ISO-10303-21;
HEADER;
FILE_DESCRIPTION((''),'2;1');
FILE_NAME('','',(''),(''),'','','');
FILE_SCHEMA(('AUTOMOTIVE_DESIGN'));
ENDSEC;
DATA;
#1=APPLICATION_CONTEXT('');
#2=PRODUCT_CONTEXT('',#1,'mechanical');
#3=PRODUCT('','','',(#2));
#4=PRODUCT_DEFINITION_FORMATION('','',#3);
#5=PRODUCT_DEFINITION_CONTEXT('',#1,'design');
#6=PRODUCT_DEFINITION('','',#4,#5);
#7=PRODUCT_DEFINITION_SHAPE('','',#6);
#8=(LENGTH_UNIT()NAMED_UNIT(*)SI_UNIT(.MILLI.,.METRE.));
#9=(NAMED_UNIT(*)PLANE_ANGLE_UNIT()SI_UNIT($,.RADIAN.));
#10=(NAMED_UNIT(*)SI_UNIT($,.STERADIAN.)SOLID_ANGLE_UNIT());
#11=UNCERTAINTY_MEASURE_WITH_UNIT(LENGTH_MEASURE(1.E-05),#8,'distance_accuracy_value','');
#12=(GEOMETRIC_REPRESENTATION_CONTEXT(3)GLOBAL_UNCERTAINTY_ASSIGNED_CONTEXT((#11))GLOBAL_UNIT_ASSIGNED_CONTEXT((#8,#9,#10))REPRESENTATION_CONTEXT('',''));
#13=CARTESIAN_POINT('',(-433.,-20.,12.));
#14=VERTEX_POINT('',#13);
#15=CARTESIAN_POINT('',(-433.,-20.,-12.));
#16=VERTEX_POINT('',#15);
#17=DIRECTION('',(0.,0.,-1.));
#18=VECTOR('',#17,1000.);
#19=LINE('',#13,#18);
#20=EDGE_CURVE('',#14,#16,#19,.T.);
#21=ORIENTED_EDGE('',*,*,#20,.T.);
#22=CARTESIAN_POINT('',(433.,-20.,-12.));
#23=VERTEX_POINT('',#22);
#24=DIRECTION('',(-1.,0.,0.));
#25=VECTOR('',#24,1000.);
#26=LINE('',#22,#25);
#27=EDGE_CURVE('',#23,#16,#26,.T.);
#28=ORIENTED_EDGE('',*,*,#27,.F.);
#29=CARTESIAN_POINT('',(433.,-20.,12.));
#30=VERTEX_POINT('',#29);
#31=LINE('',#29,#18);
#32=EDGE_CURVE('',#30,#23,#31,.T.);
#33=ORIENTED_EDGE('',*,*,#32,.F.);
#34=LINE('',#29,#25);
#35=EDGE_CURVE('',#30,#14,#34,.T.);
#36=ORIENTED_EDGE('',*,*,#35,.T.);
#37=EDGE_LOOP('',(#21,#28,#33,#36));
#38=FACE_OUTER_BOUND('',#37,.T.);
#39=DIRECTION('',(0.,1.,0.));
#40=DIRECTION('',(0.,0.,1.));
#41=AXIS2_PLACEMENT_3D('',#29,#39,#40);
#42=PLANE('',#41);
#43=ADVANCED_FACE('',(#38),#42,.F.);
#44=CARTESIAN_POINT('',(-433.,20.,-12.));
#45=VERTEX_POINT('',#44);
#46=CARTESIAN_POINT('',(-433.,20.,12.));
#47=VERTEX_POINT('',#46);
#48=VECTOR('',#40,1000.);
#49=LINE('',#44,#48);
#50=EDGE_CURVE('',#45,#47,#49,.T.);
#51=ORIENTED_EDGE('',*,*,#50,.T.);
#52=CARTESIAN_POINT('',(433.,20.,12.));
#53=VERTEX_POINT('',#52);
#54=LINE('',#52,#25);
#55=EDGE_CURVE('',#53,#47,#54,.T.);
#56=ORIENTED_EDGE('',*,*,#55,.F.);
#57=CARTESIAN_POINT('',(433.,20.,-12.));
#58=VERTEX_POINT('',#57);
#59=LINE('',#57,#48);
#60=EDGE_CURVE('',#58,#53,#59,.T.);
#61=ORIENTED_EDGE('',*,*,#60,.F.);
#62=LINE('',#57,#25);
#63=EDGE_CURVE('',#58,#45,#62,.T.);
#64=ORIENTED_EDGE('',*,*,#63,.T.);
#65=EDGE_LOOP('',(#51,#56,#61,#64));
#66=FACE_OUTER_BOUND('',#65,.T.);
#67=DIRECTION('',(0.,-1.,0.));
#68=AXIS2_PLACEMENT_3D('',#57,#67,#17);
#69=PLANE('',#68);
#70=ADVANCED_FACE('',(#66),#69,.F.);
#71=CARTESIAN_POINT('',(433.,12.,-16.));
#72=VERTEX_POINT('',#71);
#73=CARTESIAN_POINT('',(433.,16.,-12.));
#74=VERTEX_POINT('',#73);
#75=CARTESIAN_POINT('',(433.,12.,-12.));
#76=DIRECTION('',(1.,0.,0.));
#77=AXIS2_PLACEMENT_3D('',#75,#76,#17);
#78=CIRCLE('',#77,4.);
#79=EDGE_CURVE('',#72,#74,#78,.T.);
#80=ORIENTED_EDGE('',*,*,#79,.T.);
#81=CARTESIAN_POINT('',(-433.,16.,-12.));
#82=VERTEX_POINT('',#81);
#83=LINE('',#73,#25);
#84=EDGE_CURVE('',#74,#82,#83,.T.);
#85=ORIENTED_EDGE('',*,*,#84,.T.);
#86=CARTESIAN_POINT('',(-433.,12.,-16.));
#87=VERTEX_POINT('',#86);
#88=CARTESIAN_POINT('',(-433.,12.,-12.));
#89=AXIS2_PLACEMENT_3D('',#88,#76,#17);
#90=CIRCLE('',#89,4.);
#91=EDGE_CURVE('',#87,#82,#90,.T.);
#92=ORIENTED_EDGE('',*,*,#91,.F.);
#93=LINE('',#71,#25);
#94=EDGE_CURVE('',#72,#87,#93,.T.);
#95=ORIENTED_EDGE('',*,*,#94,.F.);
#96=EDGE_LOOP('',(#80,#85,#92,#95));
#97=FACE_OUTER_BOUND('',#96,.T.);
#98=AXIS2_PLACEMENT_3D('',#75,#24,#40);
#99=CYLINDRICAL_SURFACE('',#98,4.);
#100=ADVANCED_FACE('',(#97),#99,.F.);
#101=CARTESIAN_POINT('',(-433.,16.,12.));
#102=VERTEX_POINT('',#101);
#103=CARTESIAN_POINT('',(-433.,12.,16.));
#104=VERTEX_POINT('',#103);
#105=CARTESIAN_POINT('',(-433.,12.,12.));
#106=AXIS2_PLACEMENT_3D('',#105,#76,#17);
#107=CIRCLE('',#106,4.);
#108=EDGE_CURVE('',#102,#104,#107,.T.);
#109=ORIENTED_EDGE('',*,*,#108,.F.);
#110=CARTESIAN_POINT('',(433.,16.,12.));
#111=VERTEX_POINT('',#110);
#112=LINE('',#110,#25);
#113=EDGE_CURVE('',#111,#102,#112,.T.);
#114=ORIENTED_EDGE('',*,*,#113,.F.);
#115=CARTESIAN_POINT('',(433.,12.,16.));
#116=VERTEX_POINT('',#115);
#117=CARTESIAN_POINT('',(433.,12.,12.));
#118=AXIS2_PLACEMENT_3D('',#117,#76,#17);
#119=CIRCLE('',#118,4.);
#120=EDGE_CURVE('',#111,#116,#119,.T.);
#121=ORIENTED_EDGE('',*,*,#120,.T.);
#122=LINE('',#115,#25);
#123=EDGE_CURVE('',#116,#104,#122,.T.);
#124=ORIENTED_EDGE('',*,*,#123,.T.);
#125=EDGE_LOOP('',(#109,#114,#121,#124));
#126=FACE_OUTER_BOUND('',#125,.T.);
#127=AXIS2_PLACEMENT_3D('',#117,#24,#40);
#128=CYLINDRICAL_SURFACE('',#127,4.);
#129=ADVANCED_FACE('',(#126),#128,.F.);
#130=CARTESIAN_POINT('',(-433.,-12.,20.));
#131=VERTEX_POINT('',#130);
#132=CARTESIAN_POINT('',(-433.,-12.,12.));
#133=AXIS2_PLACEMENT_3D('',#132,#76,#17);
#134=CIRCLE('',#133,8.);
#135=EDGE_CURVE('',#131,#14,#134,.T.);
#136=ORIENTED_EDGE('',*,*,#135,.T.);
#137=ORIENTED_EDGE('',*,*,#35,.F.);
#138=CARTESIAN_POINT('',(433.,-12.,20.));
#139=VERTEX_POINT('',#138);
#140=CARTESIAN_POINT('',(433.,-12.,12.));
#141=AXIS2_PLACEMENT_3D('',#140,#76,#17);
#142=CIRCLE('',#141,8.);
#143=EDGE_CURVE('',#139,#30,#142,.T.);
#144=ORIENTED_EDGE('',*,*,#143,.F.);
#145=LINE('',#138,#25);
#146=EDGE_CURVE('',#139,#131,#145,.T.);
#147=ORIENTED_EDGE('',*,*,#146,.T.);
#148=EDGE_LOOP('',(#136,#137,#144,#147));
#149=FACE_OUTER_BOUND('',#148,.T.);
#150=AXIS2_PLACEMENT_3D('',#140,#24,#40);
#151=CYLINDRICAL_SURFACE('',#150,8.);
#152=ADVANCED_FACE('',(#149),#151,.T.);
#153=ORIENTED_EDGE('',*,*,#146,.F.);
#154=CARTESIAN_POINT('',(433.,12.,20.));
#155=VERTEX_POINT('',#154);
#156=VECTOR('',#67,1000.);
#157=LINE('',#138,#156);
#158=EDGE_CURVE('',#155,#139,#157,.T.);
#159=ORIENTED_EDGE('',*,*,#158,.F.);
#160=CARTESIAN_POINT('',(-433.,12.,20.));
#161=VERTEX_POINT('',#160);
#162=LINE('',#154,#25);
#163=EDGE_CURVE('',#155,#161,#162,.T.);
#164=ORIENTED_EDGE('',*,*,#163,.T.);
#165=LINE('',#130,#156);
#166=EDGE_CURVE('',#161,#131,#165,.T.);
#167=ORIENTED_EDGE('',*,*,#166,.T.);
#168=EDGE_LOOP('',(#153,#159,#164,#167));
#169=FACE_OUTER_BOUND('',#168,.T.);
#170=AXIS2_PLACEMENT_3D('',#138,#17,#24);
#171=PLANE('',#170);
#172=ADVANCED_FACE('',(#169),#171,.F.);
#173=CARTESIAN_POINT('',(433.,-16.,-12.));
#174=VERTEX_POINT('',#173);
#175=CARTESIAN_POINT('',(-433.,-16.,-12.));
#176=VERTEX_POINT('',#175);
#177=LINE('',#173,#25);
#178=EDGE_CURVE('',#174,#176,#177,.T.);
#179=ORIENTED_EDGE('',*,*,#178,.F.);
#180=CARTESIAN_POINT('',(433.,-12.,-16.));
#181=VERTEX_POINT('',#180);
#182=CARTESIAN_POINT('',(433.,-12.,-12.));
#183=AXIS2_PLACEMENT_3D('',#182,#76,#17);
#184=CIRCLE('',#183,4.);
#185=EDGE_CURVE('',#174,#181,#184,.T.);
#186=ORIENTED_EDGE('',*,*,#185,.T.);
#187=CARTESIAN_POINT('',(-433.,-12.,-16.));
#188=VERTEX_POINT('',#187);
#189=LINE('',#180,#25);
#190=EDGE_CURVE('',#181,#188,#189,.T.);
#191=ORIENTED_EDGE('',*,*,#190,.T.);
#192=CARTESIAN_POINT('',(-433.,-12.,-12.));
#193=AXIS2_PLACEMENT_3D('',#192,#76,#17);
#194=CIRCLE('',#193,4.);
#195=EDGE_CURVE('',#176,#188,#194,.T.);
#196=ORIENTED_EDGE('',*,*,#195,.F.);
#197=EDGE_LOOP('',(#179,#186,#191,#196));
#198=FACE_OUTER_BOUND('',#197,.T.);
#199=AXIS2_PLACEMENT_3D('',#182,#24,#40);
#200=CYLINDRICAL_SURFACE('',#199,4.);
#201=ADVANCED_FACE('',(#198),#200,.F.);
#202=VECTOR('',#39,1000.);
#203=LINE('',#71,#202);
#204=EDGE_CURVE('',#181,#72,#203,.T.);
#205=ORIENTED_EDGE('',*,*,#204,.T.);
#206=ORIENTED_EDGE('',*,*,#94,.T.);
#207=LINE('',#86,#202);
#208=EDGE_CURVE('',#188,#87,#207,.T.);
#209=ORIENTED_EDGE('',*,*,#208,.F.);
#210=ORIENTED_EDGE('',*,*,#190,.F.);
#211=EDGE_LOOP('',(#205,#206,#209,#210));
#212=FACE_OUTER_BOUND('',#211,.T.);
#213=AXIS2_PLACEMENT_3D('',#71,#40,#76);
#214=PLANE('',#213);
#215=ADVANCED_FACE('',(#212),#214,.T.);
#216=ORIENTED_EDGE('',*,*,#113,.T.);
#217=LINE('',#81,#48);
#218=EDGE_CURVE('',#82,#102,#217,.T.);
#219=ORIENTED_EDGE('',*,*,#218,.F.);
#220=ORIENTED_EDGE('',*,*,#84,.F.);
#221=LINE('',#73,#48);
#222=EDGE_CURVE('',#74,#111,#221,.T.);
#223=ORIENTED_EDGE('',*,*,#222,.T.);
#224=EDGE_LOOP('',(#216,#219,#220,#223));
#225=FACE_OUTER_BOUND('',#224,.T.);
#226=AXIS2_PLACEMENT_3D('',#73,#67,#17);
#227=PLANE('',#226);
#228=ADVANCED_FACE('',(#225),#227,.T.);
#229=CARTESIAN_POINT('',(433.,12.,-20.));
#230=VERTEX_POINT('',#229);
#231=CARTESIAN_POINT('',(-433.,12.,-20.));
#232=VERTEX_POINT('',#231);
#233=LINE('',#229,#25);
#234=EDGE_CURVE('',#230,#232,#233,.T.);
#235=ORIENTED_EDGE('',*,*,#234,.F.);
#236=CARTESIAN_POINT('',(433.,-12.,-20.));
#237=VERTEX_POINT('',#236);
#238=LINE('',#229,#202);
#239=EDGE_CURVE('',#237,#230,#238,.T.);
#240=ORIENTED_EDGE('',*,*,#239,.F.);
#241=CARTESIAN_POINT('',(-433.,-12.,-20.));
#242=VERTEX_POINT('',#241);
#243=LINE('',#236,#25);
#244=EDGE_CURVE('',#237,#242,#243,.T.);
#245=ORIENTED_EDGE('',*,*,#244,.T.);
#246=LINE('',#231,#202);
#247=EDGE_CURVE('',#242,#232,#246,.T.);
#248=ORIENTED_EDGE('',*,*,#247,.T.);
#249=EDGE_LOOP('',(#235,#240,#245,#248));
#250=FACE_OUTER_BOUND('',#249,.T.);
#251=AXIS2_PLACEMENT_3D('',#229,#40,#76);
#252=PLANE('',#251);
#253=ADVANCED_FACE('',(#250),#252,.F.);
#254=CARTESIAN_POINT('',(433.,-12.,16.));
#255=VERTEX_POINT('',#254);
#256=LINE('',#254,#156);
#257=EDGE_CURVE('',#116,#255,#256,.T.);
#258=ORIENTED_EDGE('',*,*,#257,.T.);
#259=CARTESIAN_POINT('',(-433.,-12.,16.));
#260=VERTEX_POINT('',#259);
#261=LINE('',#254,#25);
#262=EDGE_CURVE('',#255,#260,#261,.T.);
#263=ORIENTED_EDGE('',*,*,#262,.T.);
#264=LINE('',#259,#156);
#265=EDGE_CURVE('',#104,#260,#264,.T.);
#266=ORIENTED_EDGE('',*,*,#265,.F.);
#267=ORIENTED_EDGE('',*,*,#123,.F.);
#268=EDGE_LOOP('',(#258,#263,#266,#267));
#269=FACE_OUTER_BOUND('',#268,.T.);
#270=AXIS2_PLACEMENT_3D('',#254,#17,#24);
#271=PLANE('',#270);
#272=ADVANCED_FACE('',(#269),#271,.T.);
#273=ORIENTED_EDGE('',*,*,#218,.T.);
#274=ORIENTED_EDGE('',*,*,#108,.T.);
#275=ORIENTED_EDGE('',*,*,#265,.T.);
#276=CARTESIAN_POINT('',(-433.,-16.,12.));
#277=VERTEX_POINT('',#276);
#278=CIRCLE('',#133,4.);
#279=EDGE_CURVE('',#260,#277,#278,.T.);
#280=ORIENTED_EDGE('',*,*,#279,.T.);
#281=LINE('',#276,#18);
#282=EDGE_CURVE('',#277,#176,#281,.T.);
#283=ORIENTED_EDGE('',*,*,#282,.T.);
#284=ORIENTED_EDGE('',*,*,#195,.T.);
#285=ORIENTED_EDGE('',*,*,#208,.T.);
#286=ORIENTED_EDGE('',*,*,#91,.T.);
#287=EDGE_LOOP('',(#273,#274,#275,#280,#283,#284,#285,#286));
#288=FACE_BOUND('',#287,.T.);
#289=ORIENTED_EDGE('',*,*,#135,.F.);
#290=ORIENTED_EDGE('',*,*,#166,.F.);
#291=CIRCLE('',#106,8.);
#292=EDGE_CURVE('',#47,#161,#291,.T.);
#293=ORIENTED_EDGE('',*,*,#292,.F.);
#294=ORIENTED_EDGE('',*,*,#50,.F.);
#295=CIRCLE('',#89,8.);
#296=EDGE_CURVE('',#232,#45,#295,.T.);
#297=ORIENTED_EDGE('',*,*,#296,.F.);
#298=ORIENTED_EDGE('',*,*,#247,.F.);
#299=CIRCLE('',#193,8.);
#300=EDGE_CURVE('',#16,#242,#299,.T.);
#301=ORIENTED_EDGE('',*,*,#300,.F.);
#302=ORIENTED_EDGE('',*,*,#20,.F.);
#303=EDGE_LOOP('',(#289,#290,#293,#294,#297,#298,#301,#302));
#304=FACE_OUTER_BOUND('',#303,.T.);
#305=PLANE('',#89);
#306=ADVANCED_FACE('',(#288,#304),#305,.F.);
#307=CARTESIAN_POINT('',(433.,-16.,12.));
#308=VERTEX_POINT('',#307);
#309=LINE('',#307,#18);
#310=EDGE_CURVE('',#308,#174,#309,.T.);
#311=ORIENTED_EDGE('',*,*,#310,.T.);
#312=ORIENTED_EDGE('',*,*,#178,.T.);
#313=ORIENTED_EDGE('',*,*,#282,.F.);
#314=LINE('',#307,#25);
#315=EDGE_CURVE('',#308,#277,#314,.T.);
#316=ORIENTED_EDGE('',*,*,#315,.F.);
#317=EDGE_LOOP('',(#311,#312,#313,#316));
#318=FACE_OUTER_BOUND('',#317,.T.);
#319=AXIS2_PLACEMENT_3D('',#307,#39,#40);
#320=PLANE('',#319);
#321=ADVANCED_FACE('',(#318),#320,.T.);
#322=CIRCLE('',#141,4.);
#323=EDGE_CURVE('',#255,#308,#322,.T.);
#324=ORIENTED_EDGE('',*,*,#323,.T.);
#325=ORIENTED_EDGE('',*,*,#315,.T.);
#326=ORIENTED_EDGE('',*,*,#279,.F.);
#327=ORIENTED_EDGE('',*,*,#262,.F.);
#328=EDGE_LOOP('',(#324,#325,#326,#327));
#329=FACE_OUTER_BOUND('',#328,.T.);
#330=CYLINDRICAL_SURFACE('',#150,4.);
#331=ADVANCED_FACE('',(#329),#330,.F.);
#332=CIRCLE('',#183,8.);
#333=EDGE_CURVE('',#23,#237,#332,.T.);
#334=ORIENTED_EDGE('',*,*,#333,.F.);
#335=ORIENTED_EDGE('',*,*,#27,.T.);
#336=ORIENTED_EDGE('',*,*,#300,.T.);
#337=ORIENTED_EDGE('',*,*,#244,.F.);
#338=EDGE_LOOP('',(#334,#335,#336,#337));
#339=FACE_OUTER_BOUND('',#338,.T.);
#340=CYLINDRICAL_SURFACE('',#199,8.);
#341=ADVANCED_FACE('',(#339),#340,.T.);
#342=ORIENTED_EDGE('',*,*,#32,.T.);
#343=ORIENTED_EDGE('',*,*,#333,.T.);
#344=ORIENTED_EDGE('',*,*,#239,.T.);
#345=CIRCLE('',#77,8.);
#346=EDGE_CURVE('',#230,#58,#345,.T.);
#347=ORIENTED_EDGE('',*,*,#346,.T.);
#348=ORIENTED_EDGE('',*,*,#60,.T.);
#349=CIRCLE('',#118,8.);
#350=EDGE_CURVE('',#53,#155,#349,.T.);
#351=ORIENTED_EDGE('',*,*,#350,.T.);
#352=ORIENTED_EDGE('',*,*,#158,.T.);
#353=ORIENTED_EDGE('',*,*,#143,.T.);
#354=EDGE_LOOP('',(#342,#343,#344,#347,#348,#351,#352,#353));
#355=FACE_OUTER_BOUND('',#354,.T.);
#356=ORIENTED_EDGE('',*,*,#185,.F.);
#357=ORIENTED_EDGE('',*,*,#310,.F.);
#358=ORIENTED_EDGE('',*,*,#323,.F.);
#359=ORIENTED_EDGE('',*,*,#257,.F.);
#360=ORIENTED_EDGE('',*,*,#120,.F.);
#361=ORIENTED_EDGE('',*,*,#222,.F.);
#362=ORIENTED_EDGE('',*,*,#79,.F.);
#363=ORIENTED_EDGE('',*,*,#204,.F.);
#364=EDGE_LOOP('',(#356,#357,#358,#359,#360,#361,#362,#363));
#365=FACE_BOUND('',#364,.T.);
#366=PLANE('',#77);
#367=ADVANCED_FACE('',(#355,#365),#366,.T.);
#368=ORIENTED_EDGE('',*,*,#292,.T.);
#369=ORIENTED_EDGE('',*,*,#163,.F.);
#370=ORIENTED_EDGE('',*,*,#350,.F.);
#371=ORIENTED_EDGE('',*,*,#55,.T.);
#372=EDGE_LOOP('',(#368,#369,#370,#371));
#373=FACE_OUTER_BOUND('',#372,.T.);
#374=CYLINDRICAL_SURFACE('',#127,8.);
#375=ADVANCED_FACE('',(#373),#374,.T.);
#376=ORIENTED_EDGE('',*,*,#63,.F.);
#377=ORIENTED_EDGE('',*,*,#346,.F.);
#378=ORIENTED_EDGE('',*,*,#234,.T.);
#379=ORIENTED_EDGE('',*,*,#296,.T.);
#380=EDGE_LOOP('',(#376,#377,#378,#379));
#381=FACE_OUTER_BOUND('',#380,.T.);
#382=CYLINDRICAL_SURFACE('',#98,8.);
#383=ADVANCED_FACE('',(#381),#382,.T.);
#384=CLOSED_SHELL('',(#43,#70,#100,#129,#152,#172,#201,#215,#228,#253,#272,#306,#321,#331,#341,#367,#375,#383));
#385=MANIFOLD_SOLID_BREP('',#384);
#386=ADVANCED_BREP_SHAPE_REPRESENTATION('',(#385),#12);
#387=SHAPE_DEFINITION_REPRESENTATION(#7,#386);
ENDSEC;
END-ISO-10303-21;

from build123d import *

# Parameters (mm, degrees)
GB_6728_1986_040_X_40_X_4_1_DEPTH = 866


with BuildPart() as part:
    # Sketch1 → Gb／6728-1986方形空心型钢 040 X 40 X 4(1) (new body)
    with BuildSketch(Plane(origin=(-433, 0, 0), x_dir=(0, 0, -1), z_dir=(1, 0, 0))):
        with BuildLine():
            Line((-12, -20), (12, -20))
            ThreePointArc((12, -20), (17.656854249, -17.656854249), (20, -12))
            Line((20, -12), (20, 12))
            ThreePointArc((20, 12), (17.656854249, 17.656854249), (12, 20))
            Line((12, 20), (-12, 20))
            ThreePointArc((-12, 20), (-17.656854249, 17.656854249), (-20, 12))
            Line((-20, 12), (-20, -12))
            ThreePointArc((-20, -12), (-17.656854249, -17.656854249), (-12, -20))
        make_face()
        with BuildLine():
            Line((-12, -16), (12, -16))
            ThreePointArc((12, -16), (14.828427125, -14.828427125), (16, -12))
            Line((16, -12), (16, 12))
            ThreePointArc((16, 12), (14.828427125, 14.828427125), (12, 16))
            Line((12, 16), (-12, 16))
            ThreePointArc((-12, 16), (-14.828427125, 14.828427125), (-16, 12))
            Line((-16, 12), (-16, -12))
            ThreePointArc((-16, -12), (-14.828427125, -14.828427125), (-12, -16))
        make_face(mode=Mode.SUBTRACT)
    extrude(amount=GB_6728_1986_040_X_40_X_4_1_DEPTH)


solid = part.part
